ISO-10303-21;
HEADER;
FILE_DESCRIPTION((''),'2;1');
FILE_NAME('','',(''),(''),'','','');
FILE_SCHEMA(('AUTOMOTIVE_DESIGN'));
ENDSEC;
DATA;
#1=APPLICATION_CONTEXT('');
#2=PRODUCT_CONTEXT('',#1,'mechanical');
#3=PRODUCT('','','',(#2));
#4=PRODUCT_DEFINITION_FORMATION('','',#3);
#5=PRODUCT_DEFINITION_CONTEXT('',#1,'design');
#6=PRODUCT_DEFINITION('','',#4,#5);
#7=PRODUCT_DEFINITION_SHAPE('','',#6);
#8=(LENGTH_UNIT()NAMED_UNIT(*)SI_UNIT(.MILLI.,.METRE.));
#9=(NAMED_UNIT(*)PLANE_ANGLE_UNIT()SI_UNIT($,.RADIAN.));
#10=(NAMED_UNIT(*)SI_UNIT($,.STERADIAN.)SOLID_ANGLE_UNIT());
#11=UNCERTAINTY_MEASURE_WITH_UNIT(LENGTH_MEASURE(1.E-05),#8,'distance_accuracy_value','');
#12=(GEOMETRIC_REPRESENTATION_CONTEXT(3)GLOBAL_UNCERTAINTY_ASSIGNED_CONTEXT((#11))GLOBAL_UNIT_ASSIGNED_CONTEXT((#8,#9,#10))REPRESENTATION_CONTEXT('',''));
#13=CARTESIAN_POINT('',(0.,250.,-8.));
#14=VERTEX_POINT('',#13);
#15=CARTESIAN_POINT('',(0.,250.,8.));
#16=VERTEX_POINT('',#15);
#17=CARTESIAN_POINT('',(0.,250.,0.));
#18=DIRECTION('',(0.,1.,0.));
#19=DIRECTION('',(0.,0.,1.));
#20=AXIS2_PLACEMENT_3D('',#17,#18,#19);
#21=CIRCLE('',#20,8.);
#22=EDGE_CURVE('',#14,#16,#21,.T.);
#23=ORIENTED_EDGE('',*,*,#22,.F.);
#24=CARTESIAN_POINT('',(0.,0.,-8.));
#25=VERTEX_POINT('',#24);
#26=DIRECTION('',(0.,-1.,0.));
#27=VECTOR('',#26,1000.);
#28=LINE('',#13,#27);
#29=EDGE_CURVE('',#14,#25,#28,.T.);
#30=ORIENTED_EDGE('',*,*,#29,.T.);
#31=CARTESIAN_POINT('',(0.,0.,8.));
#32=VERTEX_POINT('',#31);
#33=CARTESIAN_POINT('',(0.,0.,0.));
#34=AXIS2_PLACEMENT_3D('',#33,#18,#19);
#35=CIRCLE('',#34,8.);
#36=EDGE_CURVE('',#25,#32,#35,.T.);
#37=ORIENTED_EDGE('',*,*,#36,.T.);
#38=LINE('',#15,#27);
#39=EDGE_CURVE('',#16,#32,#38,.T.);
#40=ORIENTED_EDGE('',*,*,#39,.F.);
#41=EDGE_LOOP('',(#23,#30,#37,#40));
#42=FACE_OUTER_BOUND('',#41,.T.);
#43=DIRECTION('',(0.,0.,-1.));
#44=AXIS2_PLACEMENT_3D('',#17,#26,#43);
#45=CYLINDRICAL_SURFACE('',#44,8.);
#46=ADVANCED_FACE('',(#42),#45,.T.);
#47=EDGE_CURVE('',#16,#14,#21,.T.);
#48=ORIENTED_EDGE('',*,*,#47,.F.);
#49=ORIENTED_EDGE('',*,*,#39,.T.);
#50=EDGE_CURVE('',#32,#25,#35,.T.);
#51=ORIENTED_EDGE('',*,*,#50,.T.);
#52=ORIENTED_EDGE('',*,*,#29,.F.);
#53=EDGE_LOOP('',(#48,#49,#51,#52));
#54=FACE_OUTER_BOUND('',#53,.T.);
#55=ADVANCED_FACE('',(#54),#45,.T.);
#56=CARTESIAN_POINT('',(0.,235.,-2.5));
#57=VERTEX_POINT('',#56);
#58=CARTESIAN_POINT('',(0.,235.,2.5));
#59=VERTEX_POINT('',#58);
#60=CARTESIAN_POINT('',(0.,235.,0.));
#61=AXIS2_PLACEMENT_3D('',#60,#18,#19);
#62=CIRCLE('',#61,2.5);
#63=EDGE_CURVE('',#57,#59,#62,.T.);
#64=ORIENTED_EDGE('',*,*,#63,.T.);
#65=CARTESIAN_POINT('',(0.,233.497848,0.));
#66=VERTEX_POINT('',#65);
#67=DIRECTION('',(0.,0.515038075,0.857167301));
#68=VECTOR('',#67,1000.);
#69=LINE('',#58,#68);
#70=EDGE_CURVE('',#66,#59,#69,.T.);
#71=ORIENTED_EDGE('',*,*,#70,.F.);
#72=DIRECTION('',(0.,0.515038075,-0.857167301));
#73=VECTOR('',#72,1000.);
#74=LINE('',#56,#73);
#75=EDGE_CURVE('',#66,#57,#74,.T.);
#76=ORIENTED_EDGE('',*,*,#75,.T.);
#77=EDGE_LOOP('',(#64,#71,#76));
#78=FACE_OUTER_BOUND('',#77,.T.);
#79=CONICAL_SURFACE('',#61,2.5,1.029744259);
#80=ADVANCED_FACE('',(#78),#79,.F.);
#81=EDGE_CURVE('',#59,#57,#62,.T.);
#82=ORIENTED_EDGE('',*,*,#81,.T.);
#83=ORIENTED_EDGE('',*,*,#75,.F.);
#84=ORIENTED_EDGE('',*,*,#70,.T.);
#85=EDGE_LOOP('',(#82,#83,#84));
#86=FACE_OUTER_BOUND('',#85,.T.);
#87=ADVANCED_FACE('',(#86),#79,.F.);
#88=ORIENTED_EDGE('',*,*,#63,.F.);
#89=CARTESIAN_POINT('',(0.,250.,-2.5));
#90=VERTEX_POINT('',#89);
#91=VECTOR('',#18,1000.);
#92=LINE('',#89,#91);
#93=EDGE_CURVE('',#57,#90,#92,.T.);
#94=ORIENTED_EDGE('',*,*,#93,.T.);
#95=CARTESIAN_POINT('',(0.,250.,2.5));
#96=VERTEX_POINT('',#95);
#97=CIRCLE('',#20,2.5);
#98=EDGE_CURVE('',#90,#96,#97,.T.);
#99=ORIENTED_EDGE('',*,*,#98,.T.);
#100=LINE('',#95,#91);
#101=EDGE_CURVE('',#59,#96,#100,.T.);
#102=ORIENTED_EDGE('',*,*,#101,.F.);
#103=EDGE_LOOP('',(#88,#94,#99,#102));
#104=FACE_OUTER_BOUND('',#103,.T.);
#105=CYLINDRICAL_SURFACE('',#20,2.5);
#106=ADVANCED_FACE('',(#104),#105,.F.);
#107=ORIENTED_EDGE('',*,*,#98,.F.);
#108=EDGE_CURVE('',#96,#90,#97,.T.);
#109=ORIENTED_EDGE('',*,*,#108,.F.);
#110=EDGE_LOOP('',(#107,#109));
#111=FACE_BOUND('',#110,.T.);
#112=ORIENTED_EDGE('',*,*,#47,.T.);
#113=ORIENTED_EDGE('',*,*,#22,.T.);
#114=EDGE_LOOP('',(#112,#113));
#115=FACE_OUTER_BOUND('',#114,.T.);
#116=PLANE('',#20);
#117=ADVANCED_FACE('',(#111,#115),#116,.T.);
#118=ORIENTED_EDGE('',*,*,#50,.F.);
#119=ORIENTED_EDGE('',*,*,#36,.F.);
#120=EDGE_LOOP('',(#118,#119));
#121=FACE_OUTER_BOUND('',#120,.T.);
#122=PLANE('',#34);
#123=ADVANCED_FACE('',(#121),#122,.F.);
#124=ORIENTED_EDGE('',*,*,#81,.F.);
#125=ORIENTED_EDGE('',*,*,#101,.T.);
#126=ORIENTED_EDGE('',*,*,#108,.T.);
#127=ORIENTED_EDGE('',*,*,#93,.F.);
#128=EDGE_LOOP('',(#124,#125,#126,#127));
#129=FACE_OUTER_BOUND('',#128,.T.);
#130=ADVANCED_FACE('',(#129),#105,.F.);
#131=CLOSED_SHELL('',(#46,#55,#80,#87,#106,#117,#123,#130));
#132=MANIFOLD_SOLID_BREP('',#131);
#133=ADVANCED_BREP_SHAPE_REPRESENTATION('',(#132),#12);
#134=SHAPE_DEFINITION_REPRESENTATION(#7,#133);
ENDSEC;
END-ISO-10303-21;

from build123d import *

# Parameters (mm, degrees)
SKETCH_1_R             = 8
EXTRUDE_1_DEPTH        = 250
HOLE_WIZARD_M6_1_D     = 5
HOLE_WIZARD_M6_1_DEPTH = 15
HOLE_WIZARD_M6_1_TIP   = 1.502151548


with BuildPart() as part:
    # 草图1 → 凸台-拉伸1 (new body)
    with BuildSketch(Plane(origin=(0, 0, 0), x_dir=(1, 0, 0), z_dir=(0, 1, 0))):
        with Locations(Location((0, 0, 0), (0, 0, 270))):
            Circle(SKETCH_1_R)
    extrude(amount=EXTRUDE_1_DEPTH)

    # M6 螺纹孔1
    with Locations(Plane(origin=(0, 250, 0), x_dir=(1, 0, 0), z_dir=(0, 1, 0))):
        with Locations((0, 0)):
            Hole(HOLE_WIZARD_M6_1_D / 2, depth=HOLE_WIZARD_M6_1_DEPTH)
            with Locations((0, 0, -(HOLE_WIZARD_M6_1_DEPTH + HOLE_WIZARD_M6_1_TIP / 2))):  # 118° drill point
                Cone(0, HOLE_WIZARD_M6_1_D / 2, HOLE_WIZARD_M6_1_TIP, mode=Mode.SUBTRACT)


solid = part.part
